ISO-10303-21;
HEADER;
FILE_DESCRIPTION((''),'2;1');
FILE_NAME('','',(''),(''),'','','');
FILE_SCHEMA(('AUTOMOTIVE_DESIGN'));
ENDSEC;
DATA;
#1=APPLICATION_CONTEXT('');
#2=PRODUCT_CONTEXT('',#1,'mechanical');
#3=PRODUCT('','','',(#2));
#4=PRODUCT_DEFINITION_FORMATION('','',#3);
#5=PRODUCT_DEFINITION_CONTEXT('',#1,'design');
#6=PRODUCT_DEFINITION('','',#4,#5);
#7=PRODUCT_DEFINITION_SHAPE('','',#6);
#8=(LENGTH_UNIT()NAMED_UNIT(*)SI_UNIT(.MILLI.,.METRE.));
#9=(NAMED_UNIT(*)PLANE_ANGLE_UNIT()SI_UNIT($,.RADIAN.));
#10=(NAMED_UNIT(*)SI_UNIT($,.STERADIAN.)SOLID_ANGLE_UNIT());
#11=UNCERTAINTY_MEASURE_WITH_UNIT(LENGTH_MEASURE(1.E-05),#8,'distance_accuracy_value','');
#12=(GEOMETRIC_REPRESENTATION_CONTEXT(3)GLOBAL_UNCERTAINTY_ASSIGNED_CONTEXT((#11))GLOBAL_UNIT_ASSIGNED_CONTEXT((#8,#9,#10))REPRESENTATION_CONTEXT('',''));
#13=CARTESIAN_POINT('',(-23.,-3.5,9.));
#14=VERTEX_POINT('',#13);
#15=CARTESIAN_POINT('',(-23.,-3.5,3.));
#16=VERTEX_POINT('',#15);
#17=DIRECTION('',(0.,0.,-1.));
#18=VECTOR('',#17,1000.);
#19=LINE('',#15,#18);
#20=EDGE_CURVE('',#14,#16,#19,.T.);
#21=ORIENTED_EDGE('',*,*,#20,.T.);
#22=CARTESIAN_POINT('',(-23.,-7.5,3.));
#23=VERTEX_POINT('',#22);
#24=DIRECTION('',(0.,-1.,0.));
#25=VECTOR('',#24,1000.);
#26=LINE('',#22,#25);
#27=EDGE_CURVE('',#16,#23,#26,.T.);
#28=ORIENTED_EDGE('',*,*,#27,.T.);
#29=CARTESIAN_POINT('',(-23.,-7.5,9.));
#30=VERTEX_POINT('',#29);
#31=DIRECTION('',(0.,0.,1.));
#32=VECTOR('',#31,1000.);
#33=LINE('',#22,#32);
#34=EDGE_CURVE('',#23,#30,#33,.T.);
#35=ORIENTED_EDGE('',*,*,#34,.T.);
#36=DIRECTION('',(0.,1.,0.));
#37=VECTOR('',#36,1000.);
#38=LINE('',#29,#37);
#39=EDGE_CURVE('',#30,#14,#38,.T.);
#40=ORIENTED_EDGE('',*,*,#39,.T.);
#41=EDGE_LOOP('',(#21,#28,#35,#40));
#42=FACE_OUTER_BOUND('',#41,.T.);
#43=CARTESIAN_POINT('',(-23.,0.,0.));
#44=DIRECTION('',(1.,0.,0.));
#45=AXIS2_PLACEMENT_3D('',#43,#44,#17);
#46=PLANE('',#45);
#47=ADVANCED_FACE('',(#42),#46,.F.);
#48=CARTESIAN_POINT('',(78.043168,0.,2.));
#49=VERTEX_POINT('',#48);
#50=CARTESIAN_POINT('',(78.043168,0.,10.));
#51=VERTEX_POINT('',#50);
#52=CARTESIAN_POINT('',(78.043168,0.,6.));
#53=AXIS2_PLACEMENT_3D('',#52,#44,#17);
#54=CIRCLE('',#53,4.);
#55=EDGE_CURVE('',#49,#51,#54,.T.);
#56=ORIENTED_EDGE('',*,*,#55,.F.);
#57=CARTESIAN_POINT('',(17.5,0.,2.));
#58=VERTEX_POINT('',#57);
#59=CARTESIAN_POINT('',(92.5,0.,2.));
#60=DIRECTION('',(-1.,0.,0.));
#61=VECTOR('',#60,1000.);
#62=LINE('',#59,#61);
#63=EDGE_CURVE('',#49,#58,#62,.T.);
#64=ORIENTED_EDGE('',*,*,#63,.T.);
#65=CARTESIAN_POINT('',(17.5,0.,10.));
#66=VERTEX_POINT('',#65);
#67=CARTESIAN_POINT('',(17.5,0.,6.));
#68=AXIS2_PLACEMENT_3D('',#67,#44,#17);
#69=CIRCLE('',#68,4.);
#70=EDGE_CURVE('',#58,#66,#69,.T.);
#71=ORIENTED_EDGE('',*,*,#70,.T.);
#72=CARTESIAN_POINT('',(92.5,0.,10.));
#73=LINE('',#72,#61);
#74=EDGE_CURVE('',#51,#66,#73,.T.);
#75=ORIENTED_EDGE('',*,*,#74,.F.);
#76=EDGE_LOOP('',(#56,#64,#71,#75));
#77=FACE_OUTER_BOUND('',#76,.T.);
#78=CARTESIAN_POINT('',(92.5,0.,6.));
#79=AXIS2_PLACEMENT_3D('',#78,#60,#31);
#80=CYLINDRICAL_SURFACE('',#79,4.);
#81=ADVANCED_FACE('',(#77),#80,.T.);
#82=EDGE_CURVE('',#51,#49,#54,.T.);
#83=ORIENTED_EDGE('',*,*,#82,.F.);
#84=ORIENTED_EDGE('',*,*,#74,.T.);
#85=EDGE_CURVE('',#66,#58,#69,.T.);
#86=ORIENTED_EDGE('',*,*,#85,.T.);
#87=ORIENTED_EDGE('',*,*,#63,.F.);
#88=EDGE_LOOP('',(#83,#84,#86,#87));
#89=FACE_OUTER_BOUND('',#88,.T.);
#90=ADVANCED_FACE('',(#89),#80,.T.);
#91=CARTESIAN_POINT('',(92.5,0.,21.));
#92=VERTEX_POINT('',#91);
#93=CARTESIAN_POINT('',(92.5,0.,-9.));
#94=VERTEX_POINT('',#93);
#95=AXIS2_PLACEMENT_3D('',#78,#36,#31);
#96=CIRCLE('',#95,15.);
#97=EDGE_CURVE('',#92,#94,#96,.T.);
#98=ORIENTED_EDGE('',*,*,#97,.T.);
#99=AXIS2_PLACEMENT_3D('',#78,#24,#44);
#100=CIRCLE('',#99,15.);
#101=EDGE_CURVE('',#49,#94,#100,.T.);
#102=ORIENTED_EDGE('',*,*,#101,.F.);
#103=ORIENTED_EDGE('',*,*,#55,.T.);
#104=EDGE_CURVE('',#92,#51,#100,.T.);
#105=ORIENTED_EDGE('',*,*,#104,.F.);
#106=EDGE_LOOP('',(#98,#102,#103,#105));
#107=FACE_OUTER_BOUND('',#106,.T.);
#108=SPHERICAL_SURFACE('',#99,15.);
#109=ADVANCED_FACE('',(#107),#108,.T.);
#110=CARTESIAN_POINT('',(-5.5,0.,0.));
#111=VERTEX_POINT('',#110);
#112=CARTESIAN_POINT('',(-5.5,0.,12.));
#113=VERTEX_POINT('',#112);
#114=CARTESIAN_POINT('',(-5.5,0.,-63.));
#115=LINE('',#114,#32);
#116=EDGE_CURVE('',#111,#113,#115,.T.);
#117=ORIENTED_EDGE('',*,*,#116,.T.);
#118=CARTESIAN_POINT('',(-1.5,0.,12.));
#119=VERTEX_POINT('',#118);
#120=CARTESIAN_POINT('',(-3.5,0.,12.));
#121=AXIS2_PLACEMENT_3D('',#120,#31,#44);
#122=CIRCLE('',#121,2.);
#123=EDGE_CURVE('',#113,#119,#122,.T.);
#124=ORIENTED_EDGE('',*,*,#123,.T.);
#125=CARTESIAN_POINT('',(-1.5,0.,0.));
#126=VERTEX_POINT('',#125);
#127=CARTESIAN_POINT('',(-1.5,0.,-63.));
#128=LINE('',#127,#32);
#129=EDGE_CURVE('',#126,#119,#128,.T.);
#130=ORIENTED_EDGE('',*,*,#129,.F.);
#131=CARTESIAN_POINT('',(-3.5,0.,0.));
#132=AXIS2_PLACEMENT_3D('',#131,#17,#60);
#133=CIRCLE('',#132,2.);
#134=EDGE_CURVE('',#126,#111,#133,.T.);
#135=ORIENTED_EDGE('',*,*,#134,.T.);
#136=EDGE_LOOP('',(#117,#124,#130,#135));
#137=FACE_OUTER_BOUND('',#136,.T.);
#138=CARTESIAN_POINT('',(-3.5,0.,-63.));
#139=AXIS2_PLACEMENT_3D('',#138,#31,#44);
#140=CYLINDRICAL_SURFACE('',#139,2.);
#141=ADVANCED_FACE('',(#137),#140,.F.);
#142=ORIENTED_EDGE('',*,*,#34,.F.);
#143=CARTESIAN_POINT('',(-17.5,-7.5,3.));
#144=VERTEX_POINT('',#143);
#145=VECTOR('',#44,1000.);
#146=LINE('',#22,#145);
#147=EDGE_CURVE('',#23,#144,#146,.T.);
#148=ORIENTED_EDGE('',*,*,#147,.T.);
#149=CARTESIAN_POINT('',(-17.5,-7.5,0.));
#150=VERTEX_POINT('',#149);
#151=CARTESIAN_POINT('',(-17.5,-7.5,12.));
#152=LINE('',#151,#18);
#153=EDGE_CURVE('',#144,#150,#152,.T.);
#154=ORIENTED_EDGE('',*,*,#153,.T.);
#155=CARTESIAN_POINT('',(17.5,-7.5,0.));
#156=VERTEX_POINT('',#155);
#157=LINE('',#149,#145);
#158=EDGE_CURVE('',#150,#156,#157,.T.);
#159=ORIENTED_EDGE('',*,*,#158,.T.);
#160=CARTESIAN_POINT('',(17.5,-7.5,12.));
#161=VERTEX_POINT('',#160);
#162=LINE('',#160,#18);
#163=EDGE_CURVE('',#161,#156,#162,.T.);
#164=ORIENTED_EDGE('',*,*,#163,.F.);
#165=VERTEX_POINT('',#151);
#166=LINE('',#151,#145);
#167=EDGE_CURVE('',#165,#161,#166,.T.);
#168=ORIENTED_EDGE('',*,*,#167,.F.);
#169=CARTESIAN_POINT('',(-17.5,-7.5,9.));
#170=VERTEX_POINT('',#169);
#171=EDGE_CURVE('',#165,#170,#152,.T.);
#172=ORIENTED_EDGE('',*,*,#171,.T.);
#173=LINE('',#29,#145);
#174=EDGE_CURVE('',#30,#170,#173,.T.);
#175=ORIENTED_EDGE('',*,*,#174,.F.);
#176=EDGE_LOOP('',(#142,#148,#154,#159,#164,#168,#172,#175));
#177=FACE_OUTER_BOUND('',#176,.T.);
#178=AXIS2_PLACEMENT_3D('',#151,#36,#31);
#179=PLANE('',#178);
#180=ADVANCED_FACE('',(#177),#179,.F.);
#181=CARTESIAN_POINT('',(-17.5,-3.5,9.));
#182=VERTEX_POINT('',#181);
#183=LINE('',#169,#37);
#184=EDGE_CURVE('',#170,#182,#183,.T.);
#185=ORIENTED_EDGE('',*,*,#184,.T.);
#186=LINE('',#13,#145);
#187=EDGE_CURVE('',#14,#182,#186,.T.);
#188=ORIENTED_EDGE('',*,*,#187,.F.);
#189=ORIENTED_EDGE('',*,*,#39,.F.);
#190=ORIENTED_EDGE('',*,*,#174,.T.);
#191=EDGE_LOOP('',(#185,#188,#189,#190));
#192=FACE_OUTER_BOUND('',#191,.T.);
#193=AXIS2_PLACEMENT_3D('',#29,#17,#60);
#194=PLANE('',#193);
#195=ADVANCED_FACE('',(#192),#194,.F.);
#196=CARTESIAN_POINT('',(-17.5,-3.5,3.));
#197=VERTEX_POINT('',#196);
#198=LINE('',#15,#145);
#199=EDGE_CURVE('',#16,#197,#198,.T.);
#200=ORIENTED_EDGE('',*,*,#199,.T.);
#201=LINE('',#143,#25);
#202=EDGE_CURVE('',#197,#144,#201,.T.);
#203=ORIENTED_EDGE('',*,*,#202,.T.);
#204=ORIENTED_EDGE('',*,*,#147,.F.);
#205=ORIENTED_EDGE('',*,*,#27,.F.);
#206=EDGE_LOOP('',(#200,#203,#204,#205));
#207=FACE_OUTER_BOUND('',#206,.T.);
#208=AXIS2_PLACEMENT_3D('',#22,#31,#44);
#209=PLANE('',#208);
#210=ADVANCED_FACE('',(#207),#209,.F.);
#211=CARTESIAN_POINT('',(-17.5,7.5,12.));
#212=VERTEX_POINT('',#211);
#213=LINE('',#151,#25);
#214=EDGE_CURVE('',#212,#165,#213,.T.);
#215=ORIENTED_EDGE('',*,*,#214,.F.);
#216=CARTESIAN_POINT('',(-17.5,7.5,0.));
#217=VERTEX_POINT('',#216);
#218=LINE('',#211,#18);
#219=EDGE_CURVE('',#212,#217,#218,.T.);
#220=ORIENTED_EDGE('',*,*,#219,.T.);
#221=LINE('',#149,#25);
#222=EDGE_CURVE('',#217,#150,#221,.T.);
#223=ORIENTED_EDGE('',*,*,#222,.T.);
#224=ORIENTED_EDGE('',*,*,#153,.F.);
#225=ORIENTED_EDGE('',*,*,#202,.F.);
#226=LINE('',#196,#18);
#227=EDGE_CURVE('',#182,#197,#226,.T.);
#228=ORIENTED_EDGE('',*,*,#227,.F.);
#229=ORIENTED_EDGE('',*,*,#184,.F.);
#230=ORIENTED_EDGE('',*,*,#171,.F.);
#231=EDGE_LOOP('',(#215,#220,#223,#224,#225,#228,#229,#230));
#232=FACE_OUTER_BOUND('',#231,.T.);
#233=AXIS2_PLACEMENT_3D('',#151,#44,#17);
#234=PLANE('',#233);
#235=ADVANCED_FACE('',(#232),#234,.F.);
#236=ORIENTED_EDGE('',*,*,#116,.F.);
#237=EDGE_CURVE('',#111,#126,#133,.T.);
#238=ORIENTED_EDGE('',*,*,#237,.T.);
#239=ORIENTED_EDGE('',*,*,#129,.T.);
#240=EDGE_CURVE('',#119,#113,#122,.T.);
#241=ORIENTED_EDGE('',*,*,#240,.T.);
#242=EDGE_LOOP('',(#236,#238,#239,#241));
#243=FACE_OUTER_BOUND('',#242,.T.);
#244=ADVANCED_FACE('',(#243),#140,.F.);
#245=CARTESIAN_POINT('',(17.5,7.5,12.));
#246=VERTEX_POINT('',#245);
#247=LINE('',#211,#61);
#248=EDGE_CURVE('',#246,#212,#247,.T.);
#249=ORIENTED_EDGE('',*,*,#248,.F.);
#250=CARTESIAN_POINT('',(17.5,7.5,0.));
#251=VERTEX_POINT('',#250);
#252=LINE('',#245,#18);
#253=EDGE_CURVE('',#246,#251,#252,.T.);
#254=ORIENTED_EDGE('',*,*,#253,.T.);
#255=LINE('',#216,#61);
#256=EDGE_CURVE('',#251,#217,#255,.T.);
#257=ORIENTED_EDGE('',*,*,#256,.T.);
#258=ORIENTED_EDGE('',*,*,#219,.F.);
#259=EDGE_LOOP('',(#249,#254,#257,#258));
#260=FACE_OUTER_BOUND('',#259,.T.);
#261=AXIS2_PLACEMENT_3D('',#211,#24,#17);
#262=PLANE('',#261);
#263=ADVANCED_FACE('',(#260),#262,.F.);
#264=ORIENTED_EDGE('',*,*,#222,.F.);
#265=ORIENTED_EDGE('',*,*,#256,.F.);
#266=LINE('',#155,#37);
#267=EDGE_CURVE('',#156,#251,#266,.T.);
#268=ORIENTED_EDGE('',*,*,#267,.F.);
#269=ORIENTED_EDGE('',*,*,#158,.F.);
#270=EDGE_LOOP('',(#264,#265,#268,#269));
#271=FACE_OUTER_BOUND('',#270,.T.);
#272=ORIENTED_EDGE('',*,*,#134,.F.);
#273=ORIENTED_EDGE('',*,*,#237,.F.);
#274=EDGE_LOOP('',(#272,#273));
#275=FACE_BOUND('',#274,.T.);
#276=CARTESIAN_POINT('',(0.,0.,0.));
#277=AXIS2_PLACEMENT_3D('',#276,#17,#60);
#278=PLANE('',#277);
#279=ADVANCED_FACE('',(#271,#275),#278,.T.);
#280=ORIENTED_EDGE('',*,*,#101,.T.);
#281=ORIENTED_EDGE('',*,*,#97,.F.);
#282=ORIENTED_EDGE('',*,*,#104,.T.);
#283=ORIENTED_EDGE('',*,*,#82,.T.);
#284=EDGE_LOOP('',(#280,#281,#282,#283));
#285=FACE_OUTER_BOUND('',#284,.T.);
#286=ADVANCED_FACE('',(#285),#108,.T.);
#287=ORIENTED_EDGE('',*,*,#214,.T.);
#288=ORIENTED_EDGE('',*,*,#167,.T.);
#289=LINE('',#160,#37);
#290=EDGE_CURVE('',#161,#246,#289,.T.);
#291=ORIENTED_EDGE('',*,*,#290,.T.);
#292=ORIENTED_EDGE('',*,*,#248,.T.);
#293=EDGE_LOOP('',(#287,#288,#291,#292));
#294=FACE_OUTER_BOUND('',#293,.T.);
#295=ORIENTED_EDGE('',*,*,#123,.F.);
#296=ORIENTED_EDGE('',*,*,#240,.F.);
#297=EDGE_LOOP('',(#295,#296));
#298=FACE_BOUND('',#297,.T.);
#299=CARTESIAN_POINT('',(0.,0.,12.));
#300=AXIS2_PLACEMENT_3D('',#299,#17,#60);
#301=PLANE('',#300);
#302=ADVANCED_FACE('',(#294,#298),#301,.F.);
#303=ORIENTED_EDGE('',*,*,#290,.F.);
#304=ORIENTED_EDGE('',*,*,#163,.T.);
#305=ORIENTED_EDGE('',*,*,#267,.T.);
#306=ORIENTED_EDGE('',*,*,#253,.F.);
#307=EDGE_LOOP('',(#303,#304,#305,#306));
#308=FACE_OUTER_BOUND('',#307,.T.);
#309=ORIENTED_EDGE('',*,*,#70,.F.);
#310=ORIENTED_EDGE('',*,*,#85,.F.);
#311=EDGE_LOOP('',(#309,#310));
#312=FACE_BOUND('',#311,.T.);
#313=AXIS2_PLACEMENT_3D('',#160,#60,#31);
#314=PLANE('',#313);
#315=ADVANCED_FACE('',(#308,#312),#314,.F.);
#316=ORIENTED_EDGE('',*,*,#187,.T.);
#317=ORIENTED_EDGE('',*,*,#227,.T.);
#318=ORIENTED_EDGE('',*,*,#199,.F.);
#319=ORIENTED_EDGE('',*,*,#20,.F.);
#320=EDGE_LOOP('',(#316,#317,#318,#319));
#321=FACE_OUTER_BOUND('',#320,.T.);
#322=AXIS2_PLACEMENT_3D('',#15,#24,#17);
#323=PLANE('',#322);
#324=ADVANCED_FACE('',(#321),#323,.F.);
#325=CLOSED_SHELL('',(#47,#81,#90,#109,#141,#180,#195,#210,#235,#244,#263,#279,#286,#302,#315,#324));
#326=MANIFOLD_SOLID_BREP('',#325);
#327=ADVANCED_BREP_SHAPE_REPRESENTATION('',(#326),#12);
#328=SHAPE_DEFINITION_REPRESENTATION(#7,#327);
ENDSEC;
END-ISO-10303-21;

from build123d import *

# Parameters (mm, degrees)
HUB_BLOCK_SKETCH_W = 35
HUB_BLOCK_SKETCH_H = 15
HUB_BLOCK_DEPTH    = 12
DRIVE_TAB_SKETCH_W = 6
DRIVE_TAB_SKETCH_H = 4
DRIVE_TAB_DEPTH    = 5.5
SHAFT_SKETCH_R     = 4
SHAFT_8_DEPTH      = 75
PIN_HOLE_SKETCH_R  = 2
PIN_HOLE_4_DEPTH   = 75


with BuildPart() as part:
    # Hub Block Sketch → Hub Block (new body)
    with BuildSketch(Plane.XY):
        Rectangle(HUB_BLOCK_SKETCH_W, HUB_BLOCK_SKETCH_H)
    extrude(amount=HUB_BLOCK_DEPTH)

    # Drive Tab Sketch → Drive Tab (add)
    with BuildSketch(Plane.ZY.offset(17.5)):
        with Locations((6, -5.5)):
            Rectangle(DRIVE_TAB_SKETCH_W, DRIVE_TAB_SKETCH_H)
    extrude(amount=DRIVE_TAB_DEPTH)

    # Shaft Sketch → Shaft Ø8 (add)
    with BuildSketch(Plane(origin=(17.5, 0, 0), x_dir=(0, 0, -1), z_dir=(1, 0, 0))):
        with Locations((-6, 0)):
            Circle(SHAFT_SKETCH_R)
    extrude(amount=SHAFT_8_DEPTH)

    # Ball Knob Sketch → Ball Knob Ø30 (revolve)
    with BuildSketch(Plane(origin=(0, 0, 0), x_dir=(1, 0, 0), z_dir=(0, 1, 0))):
        with BuildLine():
            Line((92.5, 9), (92.5, -21))
            ThreePointArc((92.5, -21), (107.5, -6), (92.5, 9))
        make_face()
    revolve(axis=Axis((92.5, 0, 0), (0, 0, 1)))

    # Pin Hole Sketch → Pin Hole Ø4 (cut)
    with BuildSketch(Plane.XY.offset(12)):
        with Locations((-3.5, 0)):
            Circle(PIN_HOLE_SKETCH_R)
    extrude(amount=-PIN_HOLE_4_DEPTH, mode=Mode.SUBTRACT)


solid = part.part
